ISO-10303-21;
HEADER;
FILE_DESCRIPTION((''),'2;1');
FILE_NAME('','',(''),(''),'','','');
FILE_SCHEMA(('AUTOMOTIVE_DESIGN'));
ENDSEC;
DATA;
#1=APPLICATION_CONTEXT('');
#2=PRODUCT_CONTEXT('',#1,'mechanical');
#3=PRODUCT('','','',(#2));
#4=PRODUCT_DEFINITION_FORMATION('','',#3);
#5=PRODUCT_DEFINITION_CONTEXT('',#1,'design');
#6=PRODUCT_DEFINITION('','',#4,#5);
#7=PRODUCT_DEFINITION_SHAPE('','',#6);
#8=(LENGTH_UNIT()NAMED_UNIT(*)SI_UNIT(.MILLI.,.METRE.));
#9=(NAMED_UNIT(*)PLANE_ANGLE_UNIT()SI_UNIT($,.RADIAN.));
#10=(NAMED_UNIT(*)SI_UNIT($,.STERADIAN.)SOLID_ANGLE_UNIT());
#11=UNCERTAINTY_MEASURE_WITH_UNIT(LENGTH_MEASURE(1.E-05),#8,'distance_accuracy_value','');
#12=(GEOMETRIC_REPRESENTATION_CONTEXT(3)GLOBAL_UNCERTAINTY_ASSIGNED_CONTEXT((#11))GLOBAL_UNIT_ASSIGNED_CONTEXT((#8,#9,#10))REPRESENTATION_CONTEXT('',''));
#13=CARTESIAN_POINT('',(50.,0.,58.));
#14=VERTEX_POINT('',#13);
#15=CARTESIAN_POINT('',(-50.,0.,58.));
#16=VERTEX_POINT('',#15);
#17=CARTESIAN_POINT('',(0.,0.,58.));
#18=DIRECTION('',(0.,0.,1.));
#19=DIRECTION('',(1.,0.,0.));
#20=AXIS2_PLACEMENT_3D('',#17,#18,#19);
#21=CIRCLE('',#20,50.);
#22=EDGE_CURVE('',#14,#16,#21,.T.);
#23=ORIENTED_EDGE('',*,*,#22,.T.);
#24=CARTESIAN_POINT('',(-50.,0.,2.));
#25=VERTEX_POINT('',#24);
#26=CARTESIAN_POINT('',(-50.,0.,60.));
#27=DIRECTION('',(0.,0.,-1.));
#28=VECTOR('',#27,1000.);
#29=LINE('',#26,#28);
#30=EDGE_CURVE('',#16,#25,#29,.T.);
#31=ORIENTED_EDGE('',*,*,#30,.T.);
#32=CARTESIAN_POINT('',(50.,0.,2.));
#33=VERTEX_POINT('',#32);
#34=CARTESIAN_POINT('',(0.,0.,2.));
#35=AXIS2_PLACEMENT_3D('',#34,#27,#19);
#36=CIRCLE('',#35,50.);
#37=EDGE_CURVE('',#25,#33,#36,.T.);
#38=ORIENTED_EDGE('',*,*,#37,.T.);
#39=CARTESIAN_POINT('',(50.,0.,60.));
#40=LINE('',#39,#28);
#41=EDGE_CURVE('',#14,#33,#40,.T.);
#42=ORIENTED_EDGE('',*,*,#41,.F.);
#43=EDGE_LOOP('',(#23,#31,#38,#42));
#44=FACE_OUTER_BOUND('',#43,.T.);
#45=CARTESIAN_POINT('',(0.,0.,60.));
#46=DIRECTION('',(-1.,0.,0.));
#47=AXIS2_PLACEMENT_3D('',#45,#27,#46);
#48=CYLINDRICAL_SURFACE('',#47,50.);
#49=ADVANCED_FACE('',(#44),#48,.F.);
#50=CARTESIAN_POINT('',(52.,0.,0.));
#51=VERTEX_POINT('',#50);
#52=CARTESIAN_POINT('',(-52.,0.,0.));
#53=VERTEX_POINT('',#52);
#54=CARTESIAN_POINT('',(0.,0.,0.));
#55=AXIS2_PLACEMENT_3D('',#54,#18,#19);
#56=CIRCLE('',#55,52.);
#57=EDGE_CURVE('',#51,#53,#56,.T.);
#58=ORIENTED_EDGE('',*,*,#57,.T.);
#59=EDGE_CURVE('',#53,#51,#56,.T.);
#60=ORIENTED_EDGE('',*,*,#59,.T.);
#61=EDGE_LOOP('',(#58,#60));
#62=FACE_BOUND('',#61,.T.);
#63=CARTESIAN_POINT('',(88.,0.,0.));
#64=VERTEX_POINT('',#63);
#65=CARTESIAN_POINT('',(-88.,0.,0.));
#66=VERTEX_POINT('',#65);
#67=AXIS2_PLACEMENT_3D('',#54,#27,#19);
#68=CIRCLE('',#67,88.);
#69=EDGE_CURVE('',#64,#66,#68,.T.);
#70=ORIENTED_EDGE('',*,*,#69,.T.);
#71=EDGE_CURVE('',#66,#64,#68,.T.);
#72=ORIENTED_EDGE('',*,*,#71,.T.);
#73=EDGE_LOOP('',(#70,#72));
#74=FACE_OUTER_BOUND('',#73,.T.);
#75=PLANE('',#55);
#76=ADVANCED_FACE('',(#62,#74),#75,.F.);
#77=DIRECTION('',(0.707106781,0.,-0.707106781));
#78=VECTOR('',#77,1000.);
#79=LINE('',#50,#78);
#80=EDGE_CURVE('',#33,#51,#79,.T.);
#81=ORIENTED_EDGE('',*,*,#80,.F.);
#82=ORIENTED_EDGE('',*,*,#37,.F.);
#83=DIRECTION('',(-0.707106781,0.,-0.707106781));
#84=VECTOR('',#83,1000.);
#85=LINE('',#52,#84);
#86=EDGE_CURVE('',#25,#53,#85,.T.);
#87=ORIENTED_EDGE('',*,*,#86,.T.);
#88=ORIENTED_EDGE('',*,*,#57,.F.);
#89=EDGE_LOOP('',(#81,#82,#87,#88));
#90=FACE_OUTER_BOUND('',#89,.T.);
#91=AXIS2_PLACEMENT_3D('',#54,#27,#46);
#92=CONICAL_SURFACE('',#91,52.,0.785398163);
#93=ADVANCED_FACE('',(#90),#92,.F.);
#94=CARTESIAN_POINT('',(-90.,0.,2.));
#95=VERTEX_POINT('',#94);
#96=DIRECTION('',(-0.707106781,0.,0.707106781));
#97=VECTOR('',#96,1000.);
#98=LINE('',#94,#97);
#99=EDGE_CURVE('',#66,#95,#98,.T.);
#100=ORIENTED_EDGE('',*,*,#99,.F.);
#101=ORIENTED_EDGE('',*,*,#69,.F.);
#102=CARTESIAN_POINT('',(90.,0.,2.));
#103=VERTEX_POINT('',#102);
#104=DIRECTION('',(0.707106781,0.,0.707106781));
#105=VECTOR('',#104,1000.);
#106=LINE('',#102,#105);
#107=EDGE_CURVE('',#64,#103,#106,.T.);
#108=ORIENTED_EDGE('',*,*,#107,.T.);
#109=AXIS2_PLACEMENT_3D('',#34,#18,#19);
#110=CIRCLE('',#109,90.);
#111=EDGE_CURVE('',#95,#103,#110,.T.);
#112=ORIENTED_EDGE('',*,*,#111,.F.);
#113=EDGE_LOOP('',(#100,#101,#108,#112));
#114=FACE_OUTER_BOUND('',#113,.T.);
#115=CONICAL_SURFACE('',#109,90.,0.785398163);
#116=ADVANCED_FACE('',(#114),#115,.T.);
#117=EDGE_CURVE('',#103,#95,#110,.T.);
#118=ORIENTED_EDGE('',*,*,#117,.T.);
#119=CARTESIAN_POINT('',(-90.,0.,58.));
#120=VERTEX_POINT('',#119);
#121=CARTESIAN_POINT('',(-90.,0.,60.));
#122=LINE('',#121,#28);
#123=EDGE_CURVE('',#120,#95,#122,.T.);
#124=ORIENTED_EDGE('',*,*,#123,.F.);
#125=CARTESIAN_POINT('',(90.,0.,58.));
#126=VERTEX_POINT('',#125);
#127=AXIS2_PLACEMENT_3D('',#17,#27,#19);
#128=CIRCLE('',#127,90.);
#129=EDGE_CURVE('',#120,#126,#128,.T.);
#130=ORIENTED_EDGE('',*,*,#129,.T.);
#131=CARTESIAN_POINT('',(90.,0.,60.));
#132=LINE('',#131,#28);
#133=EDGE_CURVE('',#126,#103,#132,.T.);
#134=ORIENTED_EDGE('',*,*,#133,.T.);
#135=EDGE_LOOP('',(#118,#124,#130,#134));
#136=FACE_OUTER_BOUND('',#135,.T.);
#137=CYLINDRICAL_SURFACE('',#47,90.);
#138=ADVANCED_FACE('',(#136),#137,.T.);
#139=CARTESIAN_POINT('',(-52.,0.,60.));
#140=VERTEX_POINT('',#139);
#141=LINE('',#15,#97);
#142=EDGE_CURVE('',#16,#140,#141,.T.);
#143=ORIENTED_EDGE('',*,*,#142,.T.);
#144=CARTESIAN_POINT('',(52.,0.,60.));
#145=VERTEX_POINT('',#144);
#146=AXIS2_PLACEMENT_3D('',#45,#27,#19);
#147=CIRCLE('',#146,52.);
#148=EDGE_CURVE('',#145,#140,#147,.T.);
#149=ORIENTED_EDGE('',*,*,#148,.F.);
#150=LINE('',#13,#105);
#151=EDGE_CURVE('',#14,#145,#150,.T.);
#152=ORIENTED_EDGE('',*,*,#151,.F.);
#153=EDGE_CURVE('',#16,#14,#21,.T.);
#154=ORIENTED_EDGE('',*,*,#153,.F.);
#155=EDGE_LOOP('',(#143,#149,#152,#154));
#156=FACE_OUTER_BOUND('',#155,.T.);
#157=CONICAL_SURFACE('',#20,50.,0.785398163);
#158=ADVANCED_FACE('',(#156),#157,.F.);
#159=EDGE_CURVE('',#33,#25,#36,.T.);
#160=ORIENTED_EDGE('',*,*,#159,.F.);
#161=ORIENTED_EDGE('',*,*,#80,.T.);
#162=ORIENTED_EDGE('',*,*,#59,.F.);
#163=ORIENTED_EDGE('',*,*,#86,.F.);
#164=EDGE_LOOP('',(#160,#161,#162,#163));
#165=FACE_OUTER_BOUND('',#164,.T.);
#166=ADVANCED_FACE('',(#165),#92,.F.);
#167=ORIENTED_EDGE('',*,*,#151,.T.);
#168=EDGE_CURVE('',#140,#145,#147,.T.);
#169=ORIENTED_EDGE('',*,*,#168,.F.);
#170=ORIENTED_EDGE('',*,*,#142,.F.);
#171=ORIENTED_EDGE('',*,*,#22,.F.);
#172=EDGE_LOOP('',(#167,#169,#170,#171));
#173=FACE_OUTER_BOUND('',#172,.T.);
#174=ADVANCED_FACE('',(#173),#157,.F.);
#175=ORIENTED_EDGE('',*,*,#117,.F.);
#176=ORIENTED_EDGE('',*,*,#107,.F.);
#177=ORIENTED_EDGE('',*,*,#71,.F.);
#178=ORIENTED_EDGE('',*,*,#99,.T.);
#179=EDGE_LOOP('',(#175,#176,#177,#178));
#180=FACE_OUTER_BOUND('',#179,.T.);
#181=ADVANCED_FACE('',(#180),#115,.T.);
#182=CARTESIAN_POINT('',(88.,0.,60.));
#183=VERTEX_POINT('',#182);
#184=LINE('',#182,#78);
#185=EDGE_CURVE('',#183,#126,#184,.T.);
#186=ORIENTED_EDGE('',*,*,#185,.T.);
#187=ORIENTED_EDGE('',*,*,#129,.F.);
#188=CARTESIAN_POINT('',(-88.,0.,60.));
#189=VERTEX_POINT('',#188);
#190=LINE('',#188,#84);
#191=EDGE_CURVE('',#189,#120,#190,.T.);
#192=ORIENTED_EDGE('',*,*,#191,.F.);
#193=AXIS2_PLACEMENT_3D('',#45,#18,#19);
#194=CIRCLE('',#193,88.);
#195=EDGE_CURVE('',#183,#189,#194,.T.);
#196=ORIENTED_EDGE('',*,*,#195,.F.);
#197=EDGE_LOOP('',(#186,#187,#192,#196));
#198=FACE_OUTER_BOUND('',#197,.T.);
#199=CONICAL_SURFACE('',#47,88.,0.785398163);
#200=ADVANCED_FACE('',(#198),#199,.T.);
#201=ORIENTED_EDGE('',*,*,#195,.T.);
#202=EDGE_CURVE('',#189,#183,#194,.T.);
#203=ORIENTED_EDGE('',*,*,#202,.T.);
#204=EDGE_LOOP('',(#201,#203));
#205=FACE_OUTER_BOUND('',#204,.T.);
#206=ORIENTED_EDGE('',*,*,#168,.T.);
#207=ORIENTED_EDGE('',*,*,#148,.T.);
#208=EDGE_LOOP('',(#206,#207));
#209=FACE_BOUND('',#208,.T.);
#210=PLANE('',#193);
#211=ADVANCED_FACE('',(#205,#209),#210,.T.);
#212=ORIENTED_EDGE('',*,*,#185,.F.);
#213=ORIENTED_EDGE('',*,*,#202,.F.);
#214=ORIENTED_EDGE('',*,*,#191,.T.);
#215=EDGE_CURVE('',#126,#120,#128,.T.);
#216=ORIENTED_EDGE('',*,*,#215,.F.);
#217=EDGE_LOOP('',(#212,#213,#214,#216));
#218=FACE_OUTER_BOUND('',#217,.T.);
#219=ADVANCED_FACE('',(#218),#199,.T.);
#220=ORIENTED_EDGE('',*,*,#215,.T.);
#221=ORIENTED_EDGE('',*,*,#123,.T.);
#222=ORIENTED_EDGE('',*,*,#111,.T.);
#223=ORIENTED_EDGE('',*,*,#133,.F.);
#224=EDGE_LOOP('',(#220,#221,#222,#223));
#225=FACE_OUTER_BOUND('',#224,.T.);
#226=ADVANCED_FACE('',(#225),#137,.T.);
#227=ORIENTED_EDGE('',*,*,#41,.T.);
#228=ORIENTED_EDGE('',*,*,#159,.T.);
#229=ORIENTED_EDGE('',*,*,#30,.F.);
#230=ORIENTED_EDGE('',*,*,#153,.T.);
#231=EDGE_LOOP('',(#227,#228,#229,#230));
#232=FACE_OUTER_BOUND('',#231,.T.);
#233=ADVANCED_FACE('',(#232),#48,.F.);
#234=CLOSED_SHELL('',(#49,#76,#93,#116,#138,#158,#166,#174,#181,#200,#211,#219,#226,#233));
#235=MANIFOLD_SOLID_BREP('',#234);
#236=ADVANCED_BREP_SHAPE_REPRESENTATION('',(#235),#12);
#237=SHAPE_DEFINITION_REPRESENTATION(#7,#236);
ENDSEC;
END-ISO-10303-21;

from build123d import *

# Parameters (mm, degrees)
SKETCH1_R           = 90
SKETCH1_R_2         = 50
BOSS_EXTRUDE1_DEPTH = 60
CHAMFER1_SIZE       = 2


with BuildPart() as part:
    # Sketch1 → Boss-Extrude1 (new body)
    with BuildSketch(Plane.XY):
        Circle(SKETCH1_R)
        Circle(SKETCH1_R_2, mode=Mode.SUBTRACT)
    extrude(amount=BOSS_EXTRUDE1_DEPTH)

    # Chamfer1
    chamfer1_edges = [part.edges().sort_by_distance(p)[0] for p in [
        (-90, 0, 0),
        (-90, 0, 60),
        (-50, 0, 0),
        (-50, 0, 60),
    ]]
    chamfer(chamfer1_edges, length=CHAMFER1_SIZE)


solid = part.part
